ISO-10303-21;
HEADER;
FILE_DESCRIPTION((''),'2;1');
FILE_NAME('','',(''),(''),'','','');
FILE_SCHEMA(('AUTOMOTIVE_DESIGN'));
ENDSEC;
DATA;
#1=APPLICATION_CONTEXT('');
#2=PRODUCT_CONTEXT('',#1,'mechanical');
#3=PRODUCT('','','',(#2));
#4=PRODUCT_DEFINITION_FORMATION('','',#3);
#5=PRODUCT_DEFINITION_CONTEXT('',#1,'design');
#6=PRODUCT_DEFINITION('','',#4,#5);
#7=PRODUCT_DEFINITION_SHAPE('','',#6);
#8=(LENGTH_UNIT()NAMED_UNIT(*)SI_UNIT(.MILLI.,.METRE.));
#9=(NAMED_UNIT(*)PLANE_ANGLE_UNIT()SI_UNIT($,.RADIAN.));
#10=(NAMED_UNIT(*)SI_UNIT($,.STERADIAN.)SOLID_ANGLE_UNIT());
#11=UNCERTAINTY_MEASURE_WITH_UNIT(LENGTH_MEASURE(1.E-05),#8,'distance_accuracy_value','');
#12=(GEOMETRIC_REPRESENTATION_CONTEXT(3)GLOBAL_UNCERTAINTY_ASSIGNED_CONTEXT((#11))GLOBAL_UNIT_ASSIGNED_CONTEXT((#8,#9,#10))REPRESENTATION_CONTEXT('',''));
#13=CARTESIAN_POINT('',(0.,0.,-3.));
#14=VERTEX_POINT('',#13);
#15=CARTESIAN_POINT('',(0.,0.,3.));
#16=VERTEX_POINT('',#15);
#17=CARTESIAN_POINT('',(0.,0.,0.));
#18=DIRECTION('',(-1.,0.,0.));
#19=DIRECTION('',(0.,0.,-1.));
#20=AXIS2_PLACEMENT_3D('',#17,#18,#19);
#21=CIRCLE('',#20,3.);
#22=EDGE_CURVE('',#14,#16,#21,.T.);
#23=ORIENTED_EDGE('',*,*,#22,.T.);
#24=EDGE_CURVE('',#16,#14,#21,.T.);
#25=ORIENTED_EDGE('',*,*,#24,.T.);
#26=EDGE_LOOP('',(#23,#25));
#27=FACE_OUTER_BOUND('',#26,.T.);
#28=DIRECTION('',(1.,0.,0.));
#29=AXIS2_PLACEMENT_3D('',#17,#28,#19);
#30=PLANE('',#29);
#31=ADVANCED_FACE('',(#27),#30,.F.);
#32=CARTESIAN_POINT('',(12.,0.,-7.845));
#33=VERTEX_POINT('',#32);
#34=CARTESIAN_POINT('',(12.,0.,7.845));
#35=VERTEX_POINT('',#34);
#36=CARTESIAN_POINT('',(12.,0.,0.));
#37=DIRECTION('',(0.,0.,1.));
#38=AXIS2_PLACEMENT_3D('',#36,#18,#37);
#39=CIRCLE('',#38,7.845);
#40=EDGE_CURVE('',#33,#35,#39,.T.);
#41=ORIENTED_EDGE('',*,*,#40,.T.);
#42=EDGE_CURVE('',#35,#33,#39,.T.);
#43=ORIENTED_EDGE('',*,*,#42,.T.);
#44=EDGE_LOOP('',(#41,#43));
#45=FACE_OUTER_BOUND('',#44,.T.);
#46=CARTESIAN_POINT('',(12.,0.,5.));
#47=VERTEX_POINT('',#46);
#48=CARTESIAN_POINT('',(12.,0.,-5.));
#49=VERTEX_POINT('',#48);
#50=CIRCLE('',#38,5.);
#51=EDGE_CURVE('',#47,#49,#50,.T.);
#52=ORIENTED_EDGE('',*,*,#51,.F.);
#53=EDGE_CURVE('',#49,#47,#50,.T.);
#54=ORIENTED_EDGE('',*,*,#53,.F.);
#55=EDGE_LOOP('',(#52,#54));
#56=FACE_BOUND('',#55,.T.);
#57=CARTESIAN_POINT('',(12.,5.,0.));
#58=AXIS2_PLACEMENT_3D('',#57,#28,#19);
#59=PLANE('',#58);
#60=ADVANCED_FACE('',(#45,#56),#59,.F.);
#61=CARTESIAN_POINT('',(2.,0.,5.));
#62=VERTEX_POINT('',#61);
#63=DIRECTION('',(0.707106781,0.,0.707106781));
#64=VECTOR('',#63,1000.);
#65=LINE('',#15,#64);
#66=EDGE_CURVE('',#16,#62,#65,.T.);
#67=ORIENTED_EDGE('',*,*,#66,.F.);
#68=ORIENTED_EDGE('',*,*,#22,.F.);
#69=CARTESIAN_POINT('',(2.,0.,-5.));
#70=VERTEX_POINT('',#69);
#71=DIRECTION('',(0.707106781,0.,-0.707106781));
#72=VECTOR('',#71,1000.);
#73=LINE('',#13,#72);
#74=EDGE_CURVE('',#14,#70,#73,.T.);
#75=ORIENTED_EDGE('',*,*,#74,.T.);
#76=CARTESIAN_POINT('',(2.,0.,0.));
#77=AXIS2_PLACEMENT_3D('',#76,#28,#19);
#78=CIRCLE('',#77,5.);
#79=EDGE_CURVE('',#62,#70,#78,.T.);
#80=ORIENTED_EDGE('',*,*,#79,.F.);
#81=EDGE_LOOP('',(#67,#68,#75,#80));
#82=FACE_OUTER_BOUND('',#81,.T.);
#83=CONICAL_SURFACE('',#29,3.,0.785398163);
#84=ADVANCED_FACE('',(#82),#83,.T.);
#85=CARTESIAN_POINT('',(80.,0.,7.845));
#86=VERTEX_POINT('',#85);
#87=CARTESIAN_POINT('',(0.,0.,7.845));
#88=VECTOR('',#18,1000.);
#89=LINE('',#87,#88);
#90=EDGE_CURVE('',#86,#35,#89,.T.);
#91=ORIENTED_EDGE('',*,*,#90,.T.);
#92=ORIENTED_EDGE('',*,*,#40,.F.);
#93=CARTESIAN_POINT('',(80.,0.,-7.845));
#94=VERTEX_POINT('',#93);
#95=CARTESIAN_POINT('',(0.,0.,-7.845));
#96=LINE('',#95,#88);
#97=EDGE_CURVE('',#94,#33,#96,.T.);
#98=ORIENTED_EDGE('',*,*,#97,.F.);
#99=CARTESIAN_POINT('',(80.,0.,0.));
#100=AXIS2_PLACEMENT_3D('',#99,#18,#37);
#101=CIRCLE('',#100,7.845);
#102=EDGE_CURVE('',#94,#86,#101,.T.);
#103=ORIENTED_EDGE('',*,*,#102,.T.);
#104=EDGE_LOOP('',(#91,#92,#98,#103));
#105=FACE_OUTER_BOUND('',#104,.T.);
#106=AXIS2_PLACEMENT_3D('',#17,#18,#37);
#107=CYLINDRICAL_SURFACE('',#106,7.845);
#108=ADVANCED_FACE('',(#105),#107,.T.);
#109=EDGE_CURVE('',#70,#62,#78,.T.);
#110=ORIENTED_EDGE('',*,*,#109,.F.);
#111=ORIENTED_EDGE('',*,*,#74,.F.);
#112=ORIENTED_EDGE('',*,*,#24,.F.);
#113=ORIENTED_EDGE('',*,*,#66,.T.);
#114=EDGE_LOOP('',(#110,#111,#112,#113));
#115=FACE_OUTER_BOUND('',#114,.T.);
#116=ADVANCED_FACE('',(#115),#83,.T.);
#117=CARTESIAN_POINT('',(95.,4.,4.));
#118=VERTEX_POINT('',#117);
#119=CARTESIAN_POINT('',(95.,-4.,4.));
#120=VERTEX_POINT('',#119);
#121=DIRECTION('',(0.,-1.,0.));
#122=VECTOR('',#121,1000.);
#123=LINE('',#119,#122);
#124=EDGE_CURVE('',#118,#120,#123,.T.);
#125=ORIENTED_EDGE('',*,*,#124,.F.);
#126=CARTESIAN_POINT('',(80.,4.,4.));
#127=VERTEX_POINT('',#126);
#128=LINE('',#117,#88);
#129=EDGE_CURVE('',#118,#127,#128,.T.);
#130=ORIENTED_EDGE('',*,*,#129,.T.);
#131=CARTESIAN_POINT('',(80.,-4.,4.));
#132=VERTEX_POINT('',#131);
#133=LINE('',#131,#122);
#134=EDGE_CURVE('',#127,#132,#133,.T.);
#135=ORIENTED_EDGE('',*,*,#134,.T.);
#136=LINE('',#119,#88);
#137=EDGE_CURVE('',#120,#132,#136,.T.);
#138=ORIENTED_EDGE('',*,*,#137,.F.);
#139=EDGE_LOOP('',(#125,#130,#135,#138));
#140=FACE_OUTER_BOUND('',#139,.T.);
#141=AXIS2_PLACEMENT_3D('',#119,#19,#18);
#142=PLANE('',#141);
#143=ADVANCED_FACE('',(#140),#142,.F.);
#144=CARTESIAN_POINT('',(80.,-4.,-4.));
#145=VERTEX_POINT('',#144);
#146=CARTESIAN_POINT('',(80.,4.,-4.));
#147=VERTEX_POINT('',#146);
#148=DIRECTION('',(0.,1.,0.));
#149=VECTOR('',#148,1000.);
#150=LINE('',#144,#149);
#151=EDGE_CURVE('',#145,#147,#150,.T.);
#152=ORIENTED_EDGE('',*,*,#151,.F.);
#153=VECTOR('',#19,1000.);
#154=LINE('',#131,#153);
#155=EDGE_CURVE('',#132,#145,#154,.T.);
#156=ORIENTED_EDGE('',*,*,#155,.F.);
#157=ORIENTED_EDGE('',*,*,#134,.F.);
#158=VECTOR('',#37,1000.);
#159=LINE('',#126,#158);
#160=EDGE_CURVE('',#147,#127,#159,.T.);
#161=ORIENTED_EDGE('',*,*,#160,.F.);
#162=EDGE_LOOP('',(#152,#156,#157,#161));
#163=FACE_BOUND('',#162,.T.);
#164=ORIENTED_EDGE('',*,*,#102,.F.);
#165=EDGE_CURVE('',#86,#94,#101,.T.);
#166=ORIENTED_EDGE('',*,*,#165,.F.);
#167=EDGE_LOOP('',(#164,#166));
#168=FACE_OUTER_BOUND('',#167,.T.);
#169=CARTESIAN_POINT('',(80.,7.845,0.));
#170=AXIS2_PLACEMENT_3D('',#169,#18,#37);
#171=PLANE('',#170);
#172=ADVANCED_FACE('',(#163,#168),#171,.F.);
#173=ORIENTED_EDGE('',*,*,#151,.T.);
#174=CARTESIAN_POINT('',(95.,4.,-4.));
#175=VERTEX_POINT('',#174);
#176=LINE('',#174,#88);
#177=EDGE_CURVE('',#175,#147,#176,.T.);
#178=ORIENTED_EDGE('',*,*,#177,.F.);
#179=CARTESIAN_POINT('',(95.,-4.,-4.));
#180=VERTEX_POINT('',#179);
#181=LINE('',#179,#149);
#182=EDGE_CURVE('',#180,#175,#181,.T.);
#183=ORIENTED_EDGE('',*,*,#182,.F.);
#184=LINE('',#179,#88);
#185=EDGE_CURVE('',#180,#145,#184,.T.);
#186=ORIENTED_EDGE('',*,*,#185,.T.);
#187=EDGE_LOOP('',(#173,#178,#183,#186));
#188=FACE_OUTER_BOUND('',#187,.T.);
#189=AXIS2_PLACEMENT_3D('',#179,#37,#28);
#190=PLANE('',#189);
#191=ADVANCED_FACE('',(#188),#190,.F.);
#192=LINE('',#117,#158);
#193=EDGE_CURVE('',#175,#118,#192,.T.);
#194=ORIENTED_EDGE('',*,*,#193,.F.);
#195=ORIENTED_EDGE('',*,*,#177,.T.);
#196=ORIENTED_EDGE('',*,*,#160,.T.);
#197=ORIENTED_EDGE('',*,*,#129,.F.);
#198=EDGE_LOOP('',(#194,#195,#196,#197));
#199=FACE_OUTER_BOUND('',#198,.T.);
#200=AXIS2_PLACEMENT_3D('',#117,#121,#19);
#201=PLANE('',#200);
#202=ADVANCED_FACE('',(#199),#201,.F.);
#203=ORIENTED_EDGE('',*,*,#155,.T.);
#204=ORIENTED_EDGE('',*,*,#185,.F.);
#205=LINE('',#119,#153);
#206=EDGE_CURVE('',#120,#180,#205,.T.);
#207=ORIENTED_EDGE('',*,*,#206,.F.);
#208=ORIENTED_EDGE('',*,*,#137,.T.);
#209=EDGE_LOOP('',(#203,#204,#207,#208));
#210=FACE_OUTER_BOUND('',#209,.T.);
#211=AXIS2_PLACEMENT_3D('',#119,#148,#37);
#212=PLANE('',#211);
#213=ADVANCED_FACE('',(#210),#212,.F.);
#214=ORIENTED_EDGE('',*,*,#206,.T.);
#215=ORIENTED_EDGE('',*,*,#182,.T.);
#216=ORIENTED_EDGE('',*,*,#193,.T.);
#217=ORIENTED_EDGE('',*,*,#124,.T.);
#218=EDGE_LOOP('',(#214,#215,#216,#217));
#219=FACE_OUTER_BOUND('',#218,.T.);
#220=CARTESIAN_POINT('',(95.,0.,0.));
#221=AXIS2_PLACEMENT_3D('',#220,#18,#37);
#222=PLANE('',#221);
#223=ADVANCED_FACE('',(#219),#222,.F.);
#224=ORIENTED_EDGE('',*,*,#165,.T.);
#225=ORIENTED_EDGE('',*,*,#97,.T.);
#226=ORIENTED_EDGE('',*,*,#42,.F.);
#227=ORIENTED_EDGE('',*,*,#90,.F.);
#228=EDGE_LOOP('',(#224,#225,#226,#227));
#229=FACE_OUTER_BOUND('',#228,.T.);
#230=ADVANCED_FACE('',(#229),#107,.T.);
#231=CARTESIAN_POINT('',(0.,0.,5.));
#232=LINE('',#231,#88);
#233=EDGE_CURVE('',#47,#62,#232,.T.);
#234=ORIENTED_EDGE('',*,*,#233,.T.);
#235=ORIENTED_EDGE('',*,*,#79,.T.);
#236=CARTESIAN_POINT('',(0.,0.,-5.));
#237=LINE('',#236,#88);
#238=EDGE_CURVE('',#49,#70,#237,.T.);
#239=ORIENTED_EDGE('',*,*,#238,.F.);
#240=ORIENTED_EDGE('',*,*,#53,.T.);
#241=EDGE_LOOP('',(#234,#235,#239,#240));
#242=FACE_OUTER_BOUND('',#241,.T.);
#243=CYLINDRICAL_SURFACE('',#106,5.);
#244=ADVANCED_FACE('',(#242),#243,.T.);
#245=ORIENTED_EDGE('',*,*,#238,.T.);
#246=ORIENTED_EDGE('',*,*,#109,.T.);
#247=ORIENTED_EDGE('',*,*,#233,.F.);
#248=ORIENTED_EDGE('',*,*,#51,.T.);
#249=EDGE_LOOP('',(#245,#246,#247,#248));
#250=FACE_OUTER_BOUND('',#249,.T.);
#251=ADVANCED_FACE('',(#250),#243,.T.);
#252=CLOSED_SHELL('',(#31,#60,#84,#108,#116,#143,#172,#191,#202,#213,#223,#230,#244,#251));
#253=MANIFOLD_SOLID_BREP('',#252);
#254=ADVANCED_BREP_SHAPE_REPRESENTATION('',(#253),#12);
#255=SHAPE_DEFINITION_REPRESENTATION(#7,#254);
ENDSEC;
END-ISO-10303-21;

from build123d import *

# Parameters (mm, degrees)
SKETCH2_W           = 8
SKETCH2_H           = 8
BOSS_EXTRUDE1_DEPTH = 15
CHAMFER1_SIZE       = 2


with BuildPart() as part:
    # Sketch1 → Revolve1 (revolve)
    with BuildSketch(Plane.XY, mode=Mode.PRIVATE) as revolve1_sk:
        Polygon((0, 0), (0, 5), (12, 5), (12, 7.845), (80, 7.845), (80, 0), align=None)
    revolve(revolve1_sk.sketch.rotate(Axis((0, 0, 0), (1, 0, 0)), 90), axis=Axis((0, 0, 0), (1, 0, 0)))

    # Sketch2 → Boss-Extrude1 (add)
    with BuildSketch(Plane(origin=(80, 0, 0), x_dir=(0, 0, -1), z_dir=(1, 0, 0))):
        Rectangle(SKETCH2_W, SKETCH2_H)
    extrude(amount=BOSS_EXTRUDE1_DEPTH)

    # Chamfer1
    chamfer1_edges = [part.edges().sort_by_distance(p)[0] for p in [
        (0, 0, -5),
    ]]
    chamfer(chamfer1_edges, length=CHAMFER1_SIZE)


solid = part.part
